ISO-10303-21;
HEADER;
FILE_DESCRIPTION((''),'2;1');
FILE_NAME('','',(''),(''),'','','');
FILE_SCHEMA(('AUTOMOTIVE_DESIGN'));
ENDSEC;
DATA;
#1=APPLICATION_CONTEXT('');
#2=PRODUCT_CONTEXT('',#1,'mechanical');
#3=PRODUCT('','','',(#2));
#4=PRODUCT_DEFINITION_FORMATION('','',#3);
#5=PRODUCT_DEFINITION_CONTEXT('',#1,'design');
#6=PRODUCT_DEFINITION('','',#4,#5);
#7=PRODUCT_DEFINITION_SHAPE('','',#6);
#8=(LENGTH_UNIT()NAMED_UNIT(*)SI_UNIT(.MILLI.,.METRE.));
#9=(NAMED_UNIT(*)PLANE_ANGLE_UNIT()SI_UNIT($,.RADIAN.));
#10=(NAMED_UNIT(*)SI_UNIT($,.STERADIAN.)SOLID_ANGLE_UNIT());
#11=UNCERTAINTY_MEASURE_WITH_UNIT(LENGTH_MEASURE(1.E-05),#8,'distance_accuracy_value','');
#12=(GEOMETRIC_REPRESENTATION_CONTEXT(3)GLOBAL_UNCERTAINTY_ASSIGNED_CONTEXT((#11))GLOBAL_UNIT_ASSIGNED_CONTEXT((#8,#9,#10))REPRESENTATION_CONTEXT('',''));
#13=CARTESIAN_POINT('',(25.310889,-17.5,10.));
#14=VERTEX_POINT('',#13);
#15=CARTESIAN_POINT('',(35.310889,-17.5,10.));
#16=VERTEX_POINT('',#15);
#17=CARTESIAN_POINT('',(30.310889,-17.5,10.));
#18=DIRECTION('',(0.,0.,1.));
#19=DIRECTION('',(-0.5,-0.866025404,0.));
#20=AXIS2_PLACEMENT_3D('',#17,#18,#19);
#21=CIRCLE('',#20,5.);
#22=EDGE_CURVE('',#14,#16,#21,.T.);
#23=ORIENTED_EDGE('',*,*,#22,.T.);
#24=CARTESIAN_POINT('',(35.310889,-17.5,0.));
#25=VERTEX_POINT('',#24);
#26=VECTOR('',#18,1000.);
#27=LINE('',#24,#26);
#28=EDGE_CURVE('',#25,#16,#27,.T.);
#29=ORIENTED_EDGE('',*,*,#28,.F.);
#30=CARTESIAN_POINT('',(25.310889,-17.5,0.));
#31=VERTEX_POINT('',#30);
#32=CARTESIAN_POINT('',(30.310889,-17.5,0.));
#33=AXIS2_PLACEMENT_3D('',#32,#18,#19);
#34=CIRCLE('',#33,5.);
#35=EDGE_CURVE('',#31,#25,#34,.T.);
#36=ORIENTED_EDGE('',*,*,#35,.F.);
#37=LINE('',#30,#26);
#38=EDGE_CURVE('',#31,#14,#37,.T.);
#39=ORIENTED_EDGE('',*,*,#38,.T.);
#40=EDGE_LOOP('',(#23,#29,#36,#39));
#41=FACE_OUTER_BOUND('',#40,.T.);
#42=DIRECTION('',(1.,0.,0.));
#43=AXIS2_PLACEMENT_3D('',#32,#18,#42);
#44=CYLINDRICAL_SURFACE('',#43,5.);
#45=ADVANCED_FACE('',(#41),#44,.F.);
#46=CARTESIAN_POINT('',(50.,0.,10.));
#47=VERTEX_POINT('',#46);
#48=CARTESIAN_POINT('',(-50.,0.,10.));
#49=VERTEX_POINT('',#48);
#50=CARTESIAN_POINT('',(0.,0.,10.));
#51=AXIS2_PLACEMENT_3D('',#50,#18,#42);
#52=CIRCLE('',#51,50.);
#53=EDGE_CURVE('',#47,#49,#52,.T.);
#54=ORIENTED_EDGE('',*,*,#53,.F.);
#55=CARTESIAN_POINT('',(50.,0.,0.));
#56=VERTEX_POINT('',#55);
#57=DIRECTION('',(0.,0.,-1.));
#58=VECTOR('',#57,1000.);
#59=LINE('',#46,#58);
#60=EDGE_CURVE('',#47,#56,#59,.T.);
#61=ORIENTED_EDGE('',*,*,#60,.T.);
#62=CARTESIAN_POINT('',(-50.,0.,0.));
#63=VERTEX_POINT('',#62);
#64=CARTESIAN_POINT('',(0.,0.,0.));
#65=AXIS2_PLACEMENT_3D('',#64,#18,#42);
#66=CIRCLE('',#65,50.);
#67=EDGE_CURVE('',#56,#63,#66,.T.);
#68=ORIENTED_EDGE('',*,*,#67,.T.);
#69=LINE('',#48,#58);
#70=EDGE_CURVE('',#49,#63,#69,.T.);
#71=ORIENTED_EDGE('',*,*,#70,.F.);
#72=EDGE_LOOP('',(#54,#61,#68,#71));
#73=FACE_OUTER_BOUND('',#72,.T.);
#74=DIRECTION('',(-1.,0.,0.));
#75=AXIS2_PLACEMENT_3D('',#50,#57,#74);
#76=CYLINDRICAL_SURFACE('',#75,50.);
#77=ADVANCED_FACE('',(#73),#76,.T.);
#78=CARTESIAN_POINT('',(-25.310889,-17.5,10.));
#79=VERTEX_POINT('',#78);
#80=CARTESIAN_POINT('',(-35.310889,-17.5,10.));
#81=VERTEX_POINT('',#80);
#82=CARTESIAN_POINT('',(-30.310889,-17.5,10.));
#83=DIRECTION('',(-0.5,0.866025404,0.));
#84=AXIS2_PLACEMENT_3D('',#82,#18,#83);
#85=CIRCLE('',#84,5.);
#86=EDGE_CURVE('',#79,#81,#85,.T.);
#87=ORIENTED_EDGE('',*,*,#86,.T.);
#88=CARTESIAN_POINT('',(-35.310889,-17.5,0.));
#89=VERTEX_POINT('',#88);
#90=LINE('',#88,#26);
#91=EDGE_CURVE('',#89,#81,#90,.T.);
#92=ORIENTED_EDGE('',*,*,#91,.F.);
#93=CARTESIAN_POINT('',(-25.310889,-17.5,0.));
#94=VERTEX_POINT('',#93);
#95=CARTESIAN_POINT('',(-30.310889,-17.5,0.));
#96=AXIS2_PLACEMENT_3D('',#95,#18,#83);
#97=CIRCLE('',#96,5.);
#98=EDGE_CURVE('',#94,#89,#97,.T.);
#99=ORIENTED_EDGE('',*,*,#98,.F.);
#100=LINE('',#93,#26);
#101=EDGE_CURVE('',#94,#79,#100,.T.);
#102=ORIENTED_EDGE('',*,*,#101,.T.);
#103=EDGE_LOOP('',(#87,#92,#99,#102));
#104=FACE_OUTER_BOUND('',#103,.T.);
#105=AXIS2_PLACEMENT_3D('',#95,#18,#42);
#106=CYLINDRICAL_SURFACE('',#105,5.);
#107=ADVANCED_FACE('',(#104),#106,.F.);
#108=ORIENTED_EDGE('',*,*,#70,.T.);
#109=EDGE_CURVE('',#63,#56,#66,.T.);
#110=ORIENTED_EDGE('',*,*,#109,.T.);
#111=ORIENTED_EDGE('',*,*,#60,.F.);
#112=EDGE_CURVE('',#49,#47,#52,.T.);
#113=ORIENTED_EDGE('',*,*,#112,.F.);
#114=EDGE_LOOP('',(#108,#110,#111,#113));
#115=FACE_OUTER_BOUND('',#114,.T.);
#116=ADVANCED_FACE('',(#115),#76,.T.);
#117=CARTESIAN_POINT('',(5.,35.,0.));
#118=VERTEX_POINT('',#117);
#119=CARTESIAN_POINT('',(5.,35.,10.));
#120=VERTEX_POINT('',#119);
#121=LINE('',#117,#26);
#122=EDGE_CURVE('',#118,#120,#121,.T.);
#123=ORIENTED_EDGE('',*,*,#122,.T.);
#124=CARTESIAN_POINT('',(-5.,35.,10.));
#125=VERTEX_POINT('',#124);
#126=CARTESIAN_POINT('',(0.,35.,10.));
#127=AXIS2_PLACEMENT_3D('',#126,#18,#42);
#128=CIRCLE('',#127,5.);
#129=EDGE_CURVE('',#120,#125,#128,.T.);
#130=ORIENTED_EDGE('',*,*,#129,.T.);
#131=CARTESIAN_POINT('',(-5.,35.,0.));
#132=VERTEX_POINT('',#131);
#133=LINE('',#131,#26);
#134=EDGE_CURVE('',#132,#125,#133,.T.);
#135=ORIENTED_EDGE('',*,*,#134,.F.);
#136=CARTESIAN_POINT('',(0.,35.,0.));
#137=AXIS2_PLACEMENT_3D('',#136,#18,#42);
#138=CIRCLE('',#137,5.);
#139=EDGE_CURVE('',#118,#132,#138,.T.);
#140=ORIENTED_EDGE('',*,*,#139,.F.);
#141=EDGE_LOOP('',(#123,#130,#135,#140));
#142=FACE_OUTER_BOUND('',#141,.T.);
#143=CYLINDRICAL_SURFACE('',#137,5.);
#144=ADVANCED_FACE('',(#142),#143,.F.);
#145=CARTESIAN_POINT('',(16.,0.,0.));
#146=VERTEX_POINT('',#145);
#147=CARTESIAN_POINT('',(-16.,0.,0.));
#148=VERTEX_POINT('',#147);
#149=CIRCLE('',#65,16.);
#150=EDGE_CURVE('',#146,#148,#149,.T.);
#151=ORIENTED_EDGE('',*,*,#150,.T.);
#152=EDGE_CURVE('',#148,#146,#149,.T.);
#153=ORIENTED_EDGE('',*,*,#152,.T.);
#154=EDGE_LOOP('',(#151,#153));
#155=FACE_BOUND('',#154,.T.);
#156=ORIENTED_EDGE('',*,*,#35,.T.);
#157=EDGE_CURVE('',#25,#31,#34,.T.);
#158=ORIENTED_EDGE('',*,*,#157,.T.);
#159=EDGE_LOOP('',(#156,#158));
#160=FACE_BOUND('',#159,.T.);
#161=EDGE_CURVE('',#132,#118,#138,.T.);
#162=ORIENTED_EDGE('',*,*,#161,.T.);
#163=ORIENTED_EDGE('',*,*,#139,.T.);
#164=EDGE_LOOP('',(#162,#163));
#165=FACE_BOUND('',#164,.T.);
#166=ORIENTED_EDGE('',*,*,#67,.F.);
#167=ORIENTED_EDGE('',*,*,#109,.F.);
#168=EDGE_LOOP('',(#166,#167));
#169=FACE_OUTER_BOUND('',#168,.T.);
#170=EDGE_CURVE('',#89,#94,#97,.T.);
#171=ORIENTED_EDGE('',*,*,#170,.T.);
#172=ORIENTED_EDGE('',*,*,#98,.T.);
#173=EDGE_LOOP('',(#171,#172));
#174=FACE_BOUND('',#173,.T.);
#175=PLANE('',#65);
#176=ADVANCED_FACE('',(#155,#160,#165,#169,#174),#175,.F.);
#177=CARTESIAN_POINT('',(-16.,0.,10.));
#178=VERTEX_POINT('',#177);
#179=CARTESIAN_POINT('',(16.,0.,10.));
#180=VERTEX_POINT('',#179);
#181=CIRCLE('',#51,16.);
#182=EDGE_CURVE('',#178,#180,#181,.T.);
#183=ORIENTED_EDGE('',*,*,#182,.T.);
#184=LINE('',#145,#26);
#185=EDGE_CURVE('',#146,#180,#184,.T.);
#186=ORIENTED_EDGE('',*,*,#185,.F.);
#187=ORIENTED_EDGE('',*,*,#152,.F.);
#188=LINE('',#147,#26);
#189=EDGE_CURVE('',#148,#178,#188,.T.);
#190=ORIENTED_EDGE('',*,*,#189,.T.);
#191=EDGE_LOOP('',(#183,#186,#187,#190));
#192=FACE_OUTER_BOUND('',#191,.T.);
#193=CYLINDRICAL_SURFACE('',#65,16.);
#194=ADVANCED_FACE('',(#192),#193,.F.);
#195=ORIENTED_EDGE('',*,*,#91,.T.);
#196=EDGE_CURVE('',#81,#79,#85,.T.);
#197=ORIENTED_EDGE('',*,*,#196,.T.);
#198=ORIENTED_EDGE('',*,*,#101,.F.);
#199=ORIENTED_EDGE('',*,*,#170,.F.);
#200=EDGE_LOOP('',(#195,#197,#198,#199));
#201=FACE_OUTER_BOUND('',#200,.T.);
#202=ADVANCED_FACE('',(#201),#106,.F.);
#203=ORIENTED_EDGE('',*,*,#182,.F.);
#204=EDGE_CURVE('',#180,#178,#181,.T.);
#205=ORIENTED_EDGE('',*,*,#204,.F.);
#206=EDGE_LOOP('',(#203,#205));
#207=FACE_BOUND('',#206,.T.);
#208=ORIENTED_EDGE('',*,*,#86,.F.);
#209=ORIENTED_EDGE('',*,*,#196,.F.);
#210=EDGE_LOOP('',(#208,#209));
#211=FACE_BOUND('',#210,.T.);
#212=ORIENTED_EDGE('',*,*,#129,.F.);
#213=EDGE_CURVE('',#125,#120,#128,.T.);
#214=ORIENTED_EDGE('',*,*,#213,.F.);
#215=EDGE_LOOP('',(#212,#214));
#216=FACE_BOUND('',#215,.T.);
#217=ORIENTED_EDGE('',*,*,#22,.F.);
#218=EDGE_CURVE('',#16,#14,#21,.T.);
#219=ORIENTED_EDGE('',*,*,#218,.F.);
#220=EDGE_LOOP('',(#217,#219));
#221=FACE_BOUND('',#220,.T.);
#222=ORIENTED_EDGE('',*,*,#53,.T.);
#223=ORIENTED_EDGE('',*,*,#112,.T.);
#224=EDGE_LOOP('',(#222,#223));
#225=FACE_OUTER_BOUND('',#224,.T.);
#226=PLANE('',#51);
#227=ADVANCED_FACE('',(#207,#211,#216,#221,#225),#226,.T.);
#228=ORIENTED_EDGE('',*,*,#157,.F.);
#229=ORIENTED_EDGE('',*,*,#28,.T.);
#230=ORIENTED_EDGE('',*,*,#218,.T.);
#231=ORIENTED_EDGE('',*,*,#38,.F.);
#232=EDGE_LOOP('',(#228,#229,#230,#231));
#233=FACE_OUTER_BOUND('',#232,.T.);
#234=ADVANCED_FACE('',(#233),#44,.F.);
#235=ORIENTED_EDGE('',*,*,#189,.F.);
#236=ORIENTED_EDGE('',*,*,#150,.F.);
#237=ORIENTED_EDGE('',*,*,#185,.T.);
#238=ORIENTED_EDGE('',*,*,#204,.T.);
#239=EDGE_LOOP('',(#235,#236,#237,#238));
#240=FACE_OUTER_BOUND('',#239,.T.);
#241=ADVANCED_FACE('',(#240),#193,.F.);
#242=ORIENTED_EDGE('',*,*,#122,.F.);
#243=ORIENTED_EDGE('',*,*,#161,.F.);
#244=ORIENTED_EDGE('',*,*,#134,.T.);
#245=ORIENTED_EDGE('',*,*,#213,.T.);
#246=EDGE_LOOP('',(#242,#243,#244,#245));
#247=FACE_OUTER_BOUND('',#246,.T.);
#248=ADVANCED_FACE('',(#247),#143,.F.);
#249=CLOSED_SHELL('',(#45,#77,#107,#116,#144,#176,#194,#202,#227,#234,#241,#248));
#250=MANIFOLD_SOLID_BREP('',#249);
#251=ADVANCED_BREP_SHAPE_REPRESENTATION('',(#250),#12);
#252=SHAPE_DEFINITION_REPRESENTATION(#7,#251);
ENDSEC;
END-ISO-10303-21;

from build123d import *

# Parameters (mm, degrees)
SKETCH1_R           = 50
BOSS_EXTRUDE1_DEPTH = 10
SKETCH2_R           = 5
CUT_EXTRUDE1_DEPTH  = 10
CIRPATTERN1_COUNT   = 3
SKETCH3_R           = 16
CUT_EXTRUDE2_DEPTH  = 10


with BuildPart() as part:
    # Sketch1 → Boss-Extrude1 (new body)
    with BuildSketch(Plane.XY):
        Circle(SKETCH1_R)
    extrude(amount=BOSS_EXTRUDE1_DEPTH)

    # Sketch2 → Cut-Extrude1 (cut)
    with BuildSketch(Plane.XY.offset(10)):
        with Locations((0, 35)):
            Circle(SKETCH2_R)
    cut_extrude1 = extrude(amount=-CUT_EXTRUDE1_DEPTH, mode=Mode.SUBTRACT)

    # CirPattern1: Cut-Extrude1 ×3 about axis
    cirpattern1_axis = Axis((0, 0, 0), (0, 0, 1))
    for i in range(1, CIRPATTERN1_COUNT):
        add(cut_extrude1.rotate(cirpattern1_axis, i * 360 / CIRPATTERN1_COUNT), mode=Mode.SUBTRACT)

    # Sketch3 → Cut-Extrude2 (cut)
    with BuildSketch(Plane.XY.offset(10)):
        Circle(SKETCH3_R)
    extrude(amount=-CUT_EXTRUDE2_DEPTH, mode=Mode.SUBTRACT)


solid = part.part
